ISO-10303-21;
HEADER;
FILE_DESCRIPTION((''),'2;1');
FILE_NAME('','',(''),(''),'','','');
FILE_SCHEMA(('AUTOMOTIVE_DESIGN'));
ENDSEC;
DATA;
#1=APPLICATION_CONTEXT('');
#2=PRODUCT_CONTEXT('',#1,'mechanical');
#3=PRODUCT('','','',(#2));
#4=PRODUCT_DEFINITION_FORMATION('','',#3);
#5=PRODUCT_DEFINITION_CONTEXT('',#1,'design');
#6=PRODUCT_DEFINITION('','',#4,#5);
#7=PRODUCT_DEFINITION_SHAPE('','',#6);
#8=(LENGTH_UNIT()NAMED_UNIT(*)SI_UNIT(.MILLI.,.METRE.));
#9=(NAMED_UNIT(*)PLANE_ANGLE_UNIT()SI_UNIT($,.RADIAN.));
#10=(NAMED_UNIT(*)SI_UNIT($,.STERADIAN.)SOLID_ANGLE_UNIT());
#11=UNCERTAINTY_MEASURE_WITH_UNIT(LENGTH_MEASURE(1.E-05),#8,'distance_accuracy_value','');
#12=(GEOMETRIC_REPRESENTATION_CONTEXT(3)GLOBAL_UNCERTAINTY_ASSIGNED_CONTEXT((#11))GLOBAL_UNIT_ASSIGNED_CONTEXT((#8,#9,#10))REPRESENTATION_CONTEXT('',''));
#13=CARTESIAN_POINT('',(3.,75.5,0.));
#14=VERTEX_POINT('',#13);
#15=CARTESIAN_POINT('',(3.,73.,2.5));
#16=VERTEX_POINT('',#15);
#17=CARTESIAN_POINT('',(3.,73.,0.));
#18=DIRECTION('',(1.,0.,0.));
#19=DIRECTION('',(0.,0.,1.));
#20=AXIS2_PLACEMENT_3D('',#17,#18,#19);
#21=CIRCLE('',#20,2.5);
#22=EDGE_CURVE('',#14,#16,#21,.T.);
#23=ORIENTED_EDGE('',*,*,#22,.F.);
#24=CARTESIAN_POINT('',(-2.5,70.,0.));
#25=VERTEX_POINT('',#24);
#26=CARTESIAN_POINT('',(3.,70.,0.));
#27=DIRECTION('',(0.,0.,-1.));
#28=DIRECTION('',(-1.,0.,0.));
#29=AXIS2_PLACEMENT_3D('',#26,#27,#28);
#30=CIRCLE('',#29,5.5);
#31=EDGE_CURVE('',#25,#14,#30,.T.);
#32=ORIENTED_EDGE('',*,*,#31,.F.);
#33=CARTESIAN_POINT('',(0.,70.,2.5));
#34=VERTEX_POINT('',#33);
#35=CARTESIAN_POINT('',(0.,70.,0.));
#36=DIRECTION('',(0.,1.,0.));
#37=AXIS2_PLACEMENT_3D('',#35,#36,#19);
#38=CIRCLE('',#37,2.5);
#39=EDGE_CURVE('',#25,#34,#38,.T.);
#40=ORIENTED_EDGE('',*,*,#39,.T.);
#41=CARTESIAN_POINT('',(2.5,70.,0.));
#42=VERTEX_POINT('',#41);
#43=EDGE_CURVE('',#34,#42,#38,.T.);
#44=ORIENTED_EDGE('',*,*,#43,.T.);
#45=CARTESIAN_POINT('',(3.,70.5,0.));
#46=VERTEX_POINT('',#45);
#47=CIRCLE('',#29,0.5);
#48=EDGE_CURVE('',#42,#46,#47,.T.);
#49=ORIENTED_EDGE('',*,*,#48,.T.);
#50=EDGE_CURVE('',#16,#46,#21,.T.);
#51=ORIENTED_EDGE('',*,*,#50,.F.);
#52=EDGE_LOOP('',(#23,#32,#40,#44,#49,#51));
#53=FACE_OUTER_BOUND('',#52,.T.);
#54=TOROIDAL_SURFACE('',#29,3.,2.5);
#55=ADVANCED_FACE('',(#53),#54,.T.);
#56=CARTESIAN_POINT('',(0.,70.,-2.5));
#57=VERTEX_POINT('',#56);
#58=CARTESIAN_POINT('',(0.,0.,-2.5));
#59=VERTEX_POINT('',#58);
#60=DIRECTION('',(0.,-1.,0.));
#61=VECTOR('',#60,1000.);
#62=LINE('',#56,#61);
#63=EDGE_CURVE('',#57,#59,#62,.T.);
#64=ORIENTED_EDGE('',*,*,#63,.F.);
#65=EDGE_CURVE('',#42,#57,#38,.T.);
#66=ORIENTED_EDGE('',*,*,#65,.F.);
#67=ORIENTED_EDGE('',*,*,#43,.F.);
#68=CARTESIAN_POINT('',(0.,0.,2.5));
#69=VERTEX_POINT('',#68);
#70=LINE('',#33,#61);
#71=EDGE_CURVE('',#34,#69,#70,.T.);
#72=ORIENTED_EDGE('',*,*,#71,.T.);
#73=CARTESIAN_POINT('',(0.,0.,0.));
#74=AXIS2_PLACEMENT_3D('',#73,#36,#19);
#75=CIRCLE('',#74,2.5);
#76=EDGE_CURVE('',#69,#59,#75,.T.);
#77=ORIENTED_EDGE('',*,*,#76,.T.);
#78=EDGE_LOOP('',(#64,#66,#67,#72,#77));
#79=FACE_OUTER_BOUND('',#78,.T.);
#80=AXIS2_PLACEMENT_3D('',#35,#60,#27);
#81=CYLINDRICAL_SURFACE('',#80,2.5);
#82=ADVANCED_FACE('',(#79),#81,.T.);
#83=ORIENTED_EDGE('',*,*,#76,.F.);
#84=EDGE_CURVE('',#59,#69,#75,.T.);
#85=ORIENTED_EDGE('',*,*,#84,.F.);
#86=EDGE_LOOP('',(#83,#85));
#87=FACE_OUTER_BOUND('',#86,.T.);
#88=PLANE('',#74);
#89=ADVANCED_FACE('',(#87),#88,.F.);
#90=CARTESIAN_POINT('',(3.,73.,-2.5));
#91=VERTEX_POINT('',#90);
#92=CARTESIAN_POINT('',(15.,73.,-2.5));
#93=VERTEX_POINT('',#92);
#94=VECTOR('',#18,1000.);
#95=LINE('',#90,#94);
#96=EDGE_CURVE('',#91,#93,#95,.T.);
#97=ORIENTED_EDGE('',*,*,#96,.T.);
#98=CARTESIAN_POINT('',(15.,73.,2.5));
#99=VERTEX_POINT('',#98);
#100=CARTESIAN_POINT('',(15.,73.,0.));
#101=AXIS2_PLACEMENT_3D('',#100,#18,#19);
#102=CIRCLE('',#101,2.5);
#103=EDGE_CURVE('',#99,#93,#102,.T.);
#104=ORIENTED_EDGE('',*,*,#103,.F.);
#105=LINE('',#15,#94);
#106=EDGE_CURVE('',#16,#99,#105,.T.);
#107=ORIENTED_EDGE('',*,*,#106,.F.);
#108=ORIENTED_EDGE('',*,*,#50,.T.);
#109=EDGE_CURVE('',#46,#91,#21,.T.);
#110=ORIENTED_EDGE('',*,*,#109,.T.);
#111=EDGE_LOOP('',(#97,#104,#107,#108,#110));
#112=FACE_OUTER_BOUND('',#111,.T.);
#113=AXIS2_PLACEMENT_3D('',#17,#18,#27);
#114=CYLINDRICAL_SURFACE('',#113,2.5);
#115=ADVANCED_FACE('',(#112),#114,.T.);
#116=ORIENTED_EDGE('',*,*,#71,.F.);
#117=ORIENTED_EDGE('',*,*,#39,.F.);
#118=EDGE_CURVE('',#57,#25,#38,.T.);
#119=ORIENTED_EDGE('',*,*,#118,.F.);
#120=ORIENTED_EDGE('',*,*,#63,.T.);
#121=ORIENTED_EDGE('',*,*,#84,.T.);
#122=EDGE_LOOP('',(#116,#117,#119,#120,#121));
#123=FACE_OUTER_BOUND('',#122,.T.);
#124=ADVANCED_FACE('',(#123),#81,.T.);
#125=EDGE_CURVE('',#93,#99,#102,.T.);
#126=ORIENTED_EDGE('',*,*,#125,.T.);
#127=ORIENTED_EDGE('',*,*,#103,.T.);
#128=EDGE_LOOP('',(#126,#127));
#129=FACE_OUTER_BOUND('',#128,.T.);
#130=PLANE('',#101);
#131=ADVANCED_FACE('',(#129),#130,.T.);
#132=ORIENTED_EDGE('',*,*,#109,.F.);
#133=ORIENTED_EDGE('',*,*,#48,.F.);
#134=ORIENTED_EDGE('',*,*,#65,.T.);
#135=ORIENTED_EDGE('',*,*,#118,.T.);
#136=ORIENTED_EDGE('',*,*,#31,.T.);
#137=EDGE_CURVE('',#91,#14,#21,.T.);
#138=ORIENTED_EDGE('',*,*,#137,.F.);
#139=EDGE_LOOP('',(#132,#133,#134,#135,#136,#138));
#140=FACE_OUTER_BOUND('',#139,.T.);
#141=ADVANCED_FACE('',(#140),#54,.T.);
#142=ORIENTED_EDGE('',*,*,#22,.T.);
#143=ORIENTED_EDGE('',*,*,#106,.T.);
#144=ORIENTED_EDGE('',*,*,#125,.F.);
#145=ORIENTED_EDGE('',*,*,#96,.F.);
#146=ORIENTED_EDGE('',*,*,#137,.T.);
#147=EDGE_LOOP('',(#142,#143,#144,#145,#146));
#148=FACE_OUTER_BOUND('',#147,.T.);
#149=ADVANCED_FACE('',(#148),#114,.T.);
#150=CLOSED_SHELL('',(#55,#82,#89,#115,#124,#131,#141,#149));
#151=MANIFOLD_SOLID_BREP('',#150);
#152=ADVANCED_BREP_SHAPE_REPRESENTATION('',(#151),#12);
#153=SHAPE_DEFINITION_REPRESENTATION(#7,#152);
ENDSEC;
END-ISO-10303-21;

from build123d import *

# Parameters (mm, degrees)
SKETCH_16_R = 2.5


with BuildPart() as part:
    # 扫描1: sweep along a path in 草图17
    with BuildLine(Plane.XY) as sweep_1_path:
        Line((0, 0), (0, 70))
        ThreePointArc((0, 70), (0.878679656, 72.121320344), (3, 73))
        Line((3, 73), (15, 73))
    # 草图16 → 扫描1 (sweep)
    with BuildSketch(Plane(origin=(0, 0, 0), x_dir=(1, 0, 0), z_dir=(0, 1, 0))):
        Circle(SKETCH_16_R)
    sweep(path=sweep_1_path.line)


solid = part.part
